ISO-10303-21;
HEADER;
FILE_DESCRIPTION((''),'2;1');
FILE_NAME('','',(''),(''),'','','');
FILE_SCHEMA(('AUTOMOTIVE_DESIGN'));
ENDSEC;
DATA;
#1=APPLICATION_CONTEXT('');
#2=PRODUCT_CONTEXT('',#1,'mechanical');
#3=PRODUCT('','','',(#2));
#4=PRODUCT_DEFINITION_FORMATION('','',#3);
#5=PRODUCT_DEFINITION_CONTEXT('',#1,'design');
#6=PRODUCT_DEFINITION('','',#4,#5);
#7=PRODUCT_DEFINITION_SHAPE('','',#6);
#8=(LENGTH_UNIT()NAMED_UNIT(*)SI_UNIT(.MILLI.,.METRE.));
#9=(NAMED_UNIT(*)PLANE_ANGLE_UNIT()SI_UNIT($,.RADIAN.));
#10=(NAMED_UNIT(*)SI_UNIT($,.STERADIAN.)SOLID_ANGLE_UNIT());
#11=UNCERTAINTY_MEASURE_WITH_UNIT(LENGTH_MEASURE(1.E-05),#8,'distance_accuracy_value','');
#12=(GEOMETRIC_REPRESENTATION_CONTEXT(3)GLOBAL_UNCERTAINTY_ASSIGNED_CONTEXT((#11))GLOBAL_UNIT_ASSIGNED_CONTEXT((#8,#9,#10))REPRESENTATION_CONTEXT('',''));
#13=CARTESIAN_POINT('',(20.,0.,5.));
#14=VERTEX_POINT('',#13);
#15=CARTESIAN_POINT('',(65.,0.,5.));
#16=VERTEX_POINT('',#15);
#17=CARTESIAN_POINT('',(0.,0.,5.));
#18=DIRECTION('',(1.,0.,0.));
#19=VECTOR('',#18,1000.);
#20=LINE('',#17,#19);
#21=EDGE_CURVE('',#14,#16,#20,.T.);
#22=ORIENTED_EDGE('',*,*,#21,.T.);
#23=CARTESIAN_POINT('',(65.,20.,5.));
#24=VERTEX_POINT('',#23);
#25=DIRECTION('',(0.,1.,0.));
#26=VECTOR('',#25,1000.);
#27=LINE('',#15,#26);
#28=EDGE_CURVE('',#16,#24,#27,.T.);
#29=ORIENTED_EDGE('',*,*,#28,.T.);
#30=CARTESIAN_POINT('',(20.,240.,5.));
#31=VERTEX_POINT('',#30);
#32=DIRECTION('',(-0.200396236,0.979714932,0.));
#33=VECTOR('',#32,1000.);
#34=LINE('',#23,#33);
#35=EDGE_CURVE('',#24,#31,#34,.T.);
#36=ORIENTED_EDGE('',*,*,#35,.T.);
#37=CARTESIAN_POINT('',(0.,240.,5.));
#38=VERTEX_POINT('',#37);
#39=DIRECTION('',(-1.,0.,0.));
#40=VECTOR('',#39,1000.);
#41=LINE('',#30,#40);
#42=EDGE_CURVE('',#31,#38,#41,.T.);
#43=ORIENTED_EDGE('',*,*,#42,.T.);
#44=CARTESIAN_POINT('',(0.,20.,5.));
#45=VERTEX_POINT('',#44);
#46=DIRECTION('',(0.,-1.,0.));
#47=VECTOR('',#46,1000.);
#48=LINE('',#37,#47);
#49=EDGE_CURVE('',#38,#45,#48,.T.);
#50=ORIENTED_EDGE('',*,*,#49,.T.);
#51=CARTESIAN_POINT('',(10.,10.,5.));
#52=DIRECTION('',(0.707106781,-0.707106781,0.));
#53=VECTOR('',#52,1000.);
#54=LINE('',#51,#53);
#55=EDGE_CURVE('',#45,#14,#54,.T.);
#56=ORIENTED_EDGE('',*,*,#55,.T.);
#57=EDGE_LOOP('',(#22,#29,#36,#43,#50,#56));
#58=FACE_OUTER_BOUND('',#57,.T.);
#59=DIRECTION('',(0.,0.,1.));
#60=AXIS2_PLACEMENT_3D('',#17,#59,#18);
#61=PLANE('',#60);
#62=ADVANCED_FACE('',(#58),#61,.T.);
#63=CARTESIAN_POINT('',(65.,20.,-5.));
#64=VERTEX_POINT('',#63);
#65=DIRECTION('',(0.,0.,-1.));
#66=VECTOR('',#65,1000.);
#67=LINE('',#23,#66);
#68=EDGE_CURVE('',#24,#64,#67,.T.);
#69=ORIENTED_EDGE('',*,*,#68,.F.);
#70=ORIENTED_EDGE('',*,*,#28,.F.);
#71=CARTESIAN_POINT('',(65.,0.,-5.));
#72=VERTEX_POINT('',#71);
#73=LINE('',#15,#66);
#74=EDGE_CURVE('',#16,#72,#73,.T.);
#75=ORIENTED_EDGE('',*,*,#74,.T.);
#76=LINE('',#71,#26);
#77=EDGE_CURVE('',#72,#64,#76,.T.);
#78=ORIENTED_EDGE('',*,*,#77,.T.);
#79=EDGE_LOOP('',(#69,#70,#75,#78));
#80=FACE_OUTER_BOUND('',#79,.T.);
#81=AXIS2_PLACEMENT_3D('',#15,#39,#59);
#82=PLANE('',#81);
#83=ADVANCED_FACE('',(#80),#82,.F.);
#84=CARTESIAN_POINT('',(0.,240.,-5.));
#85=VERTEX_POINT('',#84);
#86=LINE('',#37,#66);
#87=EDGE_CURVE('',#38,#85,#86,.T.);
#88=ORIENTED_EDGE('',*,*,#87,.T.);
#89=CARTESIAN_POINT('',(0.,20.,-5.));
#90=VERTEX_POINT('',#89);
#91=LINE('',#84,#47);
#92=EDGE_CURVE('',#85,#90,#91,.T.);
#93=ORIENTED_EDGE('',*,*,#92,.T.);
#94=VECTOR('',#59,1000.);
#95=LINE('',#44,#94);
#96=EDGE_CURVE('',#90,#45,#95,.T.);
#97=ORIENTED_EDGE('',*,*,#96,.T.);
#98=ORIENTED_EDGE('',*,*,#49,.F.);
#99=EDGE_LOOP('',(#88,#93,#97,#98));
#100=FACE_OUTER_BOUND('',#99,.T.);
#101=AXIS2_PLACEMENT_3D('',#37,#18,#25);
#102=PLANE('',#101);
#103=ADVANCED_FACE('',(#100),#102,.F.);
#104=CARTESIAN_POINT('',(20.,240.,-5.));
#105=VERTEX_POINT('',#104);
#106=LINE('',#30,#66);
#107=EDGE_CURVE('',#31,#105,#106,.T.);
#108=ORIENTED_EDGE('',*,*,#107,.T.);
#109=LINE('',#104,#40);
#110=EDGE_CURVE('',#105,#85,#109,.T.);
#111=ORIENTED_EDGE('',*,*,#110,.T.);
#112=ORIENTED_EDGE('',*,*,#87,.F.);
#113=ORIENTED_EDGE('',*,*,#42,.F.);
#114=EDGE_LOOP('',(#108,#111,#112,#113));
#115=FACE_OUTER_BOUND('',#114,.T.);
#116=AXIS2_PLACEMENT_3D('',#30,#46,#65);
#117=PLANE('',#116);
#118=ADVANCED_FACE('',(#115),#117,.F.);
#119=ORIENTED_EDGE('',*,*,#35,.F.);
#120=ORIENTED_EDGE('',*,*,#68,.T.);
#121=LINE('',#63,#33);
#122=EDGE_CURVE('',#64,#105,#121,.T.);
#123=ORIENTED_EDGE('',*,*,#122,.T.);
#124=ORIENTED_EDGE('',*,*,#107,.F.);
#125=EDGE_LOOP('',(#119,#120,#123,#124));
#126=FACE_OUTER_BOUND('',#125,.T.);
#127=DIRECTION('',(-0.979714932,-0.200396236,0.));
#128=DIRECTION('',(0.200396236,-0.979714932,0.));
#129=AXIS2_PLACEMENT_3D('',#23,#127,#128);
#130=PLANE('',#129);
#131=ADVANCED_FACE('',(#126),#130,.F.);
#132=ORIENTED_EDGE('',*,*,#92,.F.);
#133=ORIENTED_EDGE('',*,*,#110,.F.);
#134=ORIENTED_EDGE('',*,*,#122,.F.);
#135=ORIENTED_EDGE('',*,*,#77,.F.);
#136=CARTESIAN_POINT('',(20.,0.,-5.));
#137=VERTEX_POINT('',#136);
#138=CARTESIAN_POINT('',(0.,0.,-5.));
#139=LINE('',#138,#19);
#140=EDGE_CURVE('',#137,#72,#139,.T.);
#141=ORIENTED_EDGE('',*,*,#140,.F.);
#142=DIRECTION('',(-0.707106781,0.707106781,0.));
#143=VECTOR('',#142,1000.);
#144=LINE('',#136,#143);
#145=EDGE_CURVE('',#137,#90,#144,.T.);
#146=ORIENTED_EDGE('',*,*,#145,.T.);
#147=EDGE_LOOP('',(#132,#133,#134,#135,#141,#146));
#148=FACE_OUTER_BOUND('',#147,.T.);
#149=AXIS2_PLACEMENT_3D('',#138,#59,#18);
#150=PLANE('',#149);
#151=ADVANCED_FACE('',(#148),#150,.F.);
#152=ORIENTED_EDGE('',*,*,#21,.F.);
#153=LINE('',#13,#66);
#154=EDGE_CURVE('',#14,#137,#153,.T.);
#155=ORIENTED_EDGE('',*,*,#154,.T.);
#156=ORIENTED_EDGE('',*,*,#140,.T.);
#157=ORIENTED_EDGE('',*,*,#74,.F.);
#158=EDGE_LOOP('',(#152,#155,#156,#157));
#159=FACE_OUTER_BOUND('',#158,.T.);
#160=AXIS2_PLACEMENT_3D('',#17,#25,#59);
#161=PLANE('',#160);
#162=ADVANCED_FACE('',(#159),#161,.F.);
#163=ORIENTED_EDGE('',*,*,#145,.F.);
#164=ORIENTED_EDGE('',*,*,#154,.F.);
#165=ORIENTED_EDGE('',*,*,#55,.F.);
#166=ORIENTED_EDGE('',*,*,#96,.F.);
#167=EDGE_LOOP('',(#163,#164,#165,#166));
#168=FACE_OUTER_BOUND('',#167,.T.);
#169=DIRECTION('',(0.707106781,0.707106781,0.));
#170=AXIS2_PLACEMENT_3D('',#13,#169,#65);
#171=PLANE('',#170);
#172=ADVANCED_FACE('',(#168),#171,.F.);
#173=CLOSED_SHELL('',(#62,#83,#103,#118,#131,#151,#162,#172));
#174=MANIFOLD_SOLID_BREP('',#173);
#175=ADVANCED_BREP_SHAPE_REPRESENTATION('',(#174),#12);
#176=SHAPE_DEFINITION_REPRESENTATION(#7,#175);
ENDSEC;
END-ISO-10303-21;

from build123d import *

# Parameters (mm, degrees)
BOSS_EXTRUDE1_DEPTH = 5
CHAMFER1_SIZE       = 20


with BuildPart() as part:
    # Sketch1 → Boss-Extrude1 (new, symmetric)
    with BuildSketch(Plane.XY):
        Polygon((0, 0), (65, 0), (65, 20), (20, 240), (0, 240), align=None)
    extrude(amount=BOSS_EXTRUDE1_DEPTH, both=True)

    # Chamfer1
    chamfer1_edges = [part.edges().sort_by_distance(p)[0] for p in [
        (0, 0, 0),
    ]]
    chamfer(chamfer1_edges, length=CHAMFER1_SIZE)


solid = part.part
